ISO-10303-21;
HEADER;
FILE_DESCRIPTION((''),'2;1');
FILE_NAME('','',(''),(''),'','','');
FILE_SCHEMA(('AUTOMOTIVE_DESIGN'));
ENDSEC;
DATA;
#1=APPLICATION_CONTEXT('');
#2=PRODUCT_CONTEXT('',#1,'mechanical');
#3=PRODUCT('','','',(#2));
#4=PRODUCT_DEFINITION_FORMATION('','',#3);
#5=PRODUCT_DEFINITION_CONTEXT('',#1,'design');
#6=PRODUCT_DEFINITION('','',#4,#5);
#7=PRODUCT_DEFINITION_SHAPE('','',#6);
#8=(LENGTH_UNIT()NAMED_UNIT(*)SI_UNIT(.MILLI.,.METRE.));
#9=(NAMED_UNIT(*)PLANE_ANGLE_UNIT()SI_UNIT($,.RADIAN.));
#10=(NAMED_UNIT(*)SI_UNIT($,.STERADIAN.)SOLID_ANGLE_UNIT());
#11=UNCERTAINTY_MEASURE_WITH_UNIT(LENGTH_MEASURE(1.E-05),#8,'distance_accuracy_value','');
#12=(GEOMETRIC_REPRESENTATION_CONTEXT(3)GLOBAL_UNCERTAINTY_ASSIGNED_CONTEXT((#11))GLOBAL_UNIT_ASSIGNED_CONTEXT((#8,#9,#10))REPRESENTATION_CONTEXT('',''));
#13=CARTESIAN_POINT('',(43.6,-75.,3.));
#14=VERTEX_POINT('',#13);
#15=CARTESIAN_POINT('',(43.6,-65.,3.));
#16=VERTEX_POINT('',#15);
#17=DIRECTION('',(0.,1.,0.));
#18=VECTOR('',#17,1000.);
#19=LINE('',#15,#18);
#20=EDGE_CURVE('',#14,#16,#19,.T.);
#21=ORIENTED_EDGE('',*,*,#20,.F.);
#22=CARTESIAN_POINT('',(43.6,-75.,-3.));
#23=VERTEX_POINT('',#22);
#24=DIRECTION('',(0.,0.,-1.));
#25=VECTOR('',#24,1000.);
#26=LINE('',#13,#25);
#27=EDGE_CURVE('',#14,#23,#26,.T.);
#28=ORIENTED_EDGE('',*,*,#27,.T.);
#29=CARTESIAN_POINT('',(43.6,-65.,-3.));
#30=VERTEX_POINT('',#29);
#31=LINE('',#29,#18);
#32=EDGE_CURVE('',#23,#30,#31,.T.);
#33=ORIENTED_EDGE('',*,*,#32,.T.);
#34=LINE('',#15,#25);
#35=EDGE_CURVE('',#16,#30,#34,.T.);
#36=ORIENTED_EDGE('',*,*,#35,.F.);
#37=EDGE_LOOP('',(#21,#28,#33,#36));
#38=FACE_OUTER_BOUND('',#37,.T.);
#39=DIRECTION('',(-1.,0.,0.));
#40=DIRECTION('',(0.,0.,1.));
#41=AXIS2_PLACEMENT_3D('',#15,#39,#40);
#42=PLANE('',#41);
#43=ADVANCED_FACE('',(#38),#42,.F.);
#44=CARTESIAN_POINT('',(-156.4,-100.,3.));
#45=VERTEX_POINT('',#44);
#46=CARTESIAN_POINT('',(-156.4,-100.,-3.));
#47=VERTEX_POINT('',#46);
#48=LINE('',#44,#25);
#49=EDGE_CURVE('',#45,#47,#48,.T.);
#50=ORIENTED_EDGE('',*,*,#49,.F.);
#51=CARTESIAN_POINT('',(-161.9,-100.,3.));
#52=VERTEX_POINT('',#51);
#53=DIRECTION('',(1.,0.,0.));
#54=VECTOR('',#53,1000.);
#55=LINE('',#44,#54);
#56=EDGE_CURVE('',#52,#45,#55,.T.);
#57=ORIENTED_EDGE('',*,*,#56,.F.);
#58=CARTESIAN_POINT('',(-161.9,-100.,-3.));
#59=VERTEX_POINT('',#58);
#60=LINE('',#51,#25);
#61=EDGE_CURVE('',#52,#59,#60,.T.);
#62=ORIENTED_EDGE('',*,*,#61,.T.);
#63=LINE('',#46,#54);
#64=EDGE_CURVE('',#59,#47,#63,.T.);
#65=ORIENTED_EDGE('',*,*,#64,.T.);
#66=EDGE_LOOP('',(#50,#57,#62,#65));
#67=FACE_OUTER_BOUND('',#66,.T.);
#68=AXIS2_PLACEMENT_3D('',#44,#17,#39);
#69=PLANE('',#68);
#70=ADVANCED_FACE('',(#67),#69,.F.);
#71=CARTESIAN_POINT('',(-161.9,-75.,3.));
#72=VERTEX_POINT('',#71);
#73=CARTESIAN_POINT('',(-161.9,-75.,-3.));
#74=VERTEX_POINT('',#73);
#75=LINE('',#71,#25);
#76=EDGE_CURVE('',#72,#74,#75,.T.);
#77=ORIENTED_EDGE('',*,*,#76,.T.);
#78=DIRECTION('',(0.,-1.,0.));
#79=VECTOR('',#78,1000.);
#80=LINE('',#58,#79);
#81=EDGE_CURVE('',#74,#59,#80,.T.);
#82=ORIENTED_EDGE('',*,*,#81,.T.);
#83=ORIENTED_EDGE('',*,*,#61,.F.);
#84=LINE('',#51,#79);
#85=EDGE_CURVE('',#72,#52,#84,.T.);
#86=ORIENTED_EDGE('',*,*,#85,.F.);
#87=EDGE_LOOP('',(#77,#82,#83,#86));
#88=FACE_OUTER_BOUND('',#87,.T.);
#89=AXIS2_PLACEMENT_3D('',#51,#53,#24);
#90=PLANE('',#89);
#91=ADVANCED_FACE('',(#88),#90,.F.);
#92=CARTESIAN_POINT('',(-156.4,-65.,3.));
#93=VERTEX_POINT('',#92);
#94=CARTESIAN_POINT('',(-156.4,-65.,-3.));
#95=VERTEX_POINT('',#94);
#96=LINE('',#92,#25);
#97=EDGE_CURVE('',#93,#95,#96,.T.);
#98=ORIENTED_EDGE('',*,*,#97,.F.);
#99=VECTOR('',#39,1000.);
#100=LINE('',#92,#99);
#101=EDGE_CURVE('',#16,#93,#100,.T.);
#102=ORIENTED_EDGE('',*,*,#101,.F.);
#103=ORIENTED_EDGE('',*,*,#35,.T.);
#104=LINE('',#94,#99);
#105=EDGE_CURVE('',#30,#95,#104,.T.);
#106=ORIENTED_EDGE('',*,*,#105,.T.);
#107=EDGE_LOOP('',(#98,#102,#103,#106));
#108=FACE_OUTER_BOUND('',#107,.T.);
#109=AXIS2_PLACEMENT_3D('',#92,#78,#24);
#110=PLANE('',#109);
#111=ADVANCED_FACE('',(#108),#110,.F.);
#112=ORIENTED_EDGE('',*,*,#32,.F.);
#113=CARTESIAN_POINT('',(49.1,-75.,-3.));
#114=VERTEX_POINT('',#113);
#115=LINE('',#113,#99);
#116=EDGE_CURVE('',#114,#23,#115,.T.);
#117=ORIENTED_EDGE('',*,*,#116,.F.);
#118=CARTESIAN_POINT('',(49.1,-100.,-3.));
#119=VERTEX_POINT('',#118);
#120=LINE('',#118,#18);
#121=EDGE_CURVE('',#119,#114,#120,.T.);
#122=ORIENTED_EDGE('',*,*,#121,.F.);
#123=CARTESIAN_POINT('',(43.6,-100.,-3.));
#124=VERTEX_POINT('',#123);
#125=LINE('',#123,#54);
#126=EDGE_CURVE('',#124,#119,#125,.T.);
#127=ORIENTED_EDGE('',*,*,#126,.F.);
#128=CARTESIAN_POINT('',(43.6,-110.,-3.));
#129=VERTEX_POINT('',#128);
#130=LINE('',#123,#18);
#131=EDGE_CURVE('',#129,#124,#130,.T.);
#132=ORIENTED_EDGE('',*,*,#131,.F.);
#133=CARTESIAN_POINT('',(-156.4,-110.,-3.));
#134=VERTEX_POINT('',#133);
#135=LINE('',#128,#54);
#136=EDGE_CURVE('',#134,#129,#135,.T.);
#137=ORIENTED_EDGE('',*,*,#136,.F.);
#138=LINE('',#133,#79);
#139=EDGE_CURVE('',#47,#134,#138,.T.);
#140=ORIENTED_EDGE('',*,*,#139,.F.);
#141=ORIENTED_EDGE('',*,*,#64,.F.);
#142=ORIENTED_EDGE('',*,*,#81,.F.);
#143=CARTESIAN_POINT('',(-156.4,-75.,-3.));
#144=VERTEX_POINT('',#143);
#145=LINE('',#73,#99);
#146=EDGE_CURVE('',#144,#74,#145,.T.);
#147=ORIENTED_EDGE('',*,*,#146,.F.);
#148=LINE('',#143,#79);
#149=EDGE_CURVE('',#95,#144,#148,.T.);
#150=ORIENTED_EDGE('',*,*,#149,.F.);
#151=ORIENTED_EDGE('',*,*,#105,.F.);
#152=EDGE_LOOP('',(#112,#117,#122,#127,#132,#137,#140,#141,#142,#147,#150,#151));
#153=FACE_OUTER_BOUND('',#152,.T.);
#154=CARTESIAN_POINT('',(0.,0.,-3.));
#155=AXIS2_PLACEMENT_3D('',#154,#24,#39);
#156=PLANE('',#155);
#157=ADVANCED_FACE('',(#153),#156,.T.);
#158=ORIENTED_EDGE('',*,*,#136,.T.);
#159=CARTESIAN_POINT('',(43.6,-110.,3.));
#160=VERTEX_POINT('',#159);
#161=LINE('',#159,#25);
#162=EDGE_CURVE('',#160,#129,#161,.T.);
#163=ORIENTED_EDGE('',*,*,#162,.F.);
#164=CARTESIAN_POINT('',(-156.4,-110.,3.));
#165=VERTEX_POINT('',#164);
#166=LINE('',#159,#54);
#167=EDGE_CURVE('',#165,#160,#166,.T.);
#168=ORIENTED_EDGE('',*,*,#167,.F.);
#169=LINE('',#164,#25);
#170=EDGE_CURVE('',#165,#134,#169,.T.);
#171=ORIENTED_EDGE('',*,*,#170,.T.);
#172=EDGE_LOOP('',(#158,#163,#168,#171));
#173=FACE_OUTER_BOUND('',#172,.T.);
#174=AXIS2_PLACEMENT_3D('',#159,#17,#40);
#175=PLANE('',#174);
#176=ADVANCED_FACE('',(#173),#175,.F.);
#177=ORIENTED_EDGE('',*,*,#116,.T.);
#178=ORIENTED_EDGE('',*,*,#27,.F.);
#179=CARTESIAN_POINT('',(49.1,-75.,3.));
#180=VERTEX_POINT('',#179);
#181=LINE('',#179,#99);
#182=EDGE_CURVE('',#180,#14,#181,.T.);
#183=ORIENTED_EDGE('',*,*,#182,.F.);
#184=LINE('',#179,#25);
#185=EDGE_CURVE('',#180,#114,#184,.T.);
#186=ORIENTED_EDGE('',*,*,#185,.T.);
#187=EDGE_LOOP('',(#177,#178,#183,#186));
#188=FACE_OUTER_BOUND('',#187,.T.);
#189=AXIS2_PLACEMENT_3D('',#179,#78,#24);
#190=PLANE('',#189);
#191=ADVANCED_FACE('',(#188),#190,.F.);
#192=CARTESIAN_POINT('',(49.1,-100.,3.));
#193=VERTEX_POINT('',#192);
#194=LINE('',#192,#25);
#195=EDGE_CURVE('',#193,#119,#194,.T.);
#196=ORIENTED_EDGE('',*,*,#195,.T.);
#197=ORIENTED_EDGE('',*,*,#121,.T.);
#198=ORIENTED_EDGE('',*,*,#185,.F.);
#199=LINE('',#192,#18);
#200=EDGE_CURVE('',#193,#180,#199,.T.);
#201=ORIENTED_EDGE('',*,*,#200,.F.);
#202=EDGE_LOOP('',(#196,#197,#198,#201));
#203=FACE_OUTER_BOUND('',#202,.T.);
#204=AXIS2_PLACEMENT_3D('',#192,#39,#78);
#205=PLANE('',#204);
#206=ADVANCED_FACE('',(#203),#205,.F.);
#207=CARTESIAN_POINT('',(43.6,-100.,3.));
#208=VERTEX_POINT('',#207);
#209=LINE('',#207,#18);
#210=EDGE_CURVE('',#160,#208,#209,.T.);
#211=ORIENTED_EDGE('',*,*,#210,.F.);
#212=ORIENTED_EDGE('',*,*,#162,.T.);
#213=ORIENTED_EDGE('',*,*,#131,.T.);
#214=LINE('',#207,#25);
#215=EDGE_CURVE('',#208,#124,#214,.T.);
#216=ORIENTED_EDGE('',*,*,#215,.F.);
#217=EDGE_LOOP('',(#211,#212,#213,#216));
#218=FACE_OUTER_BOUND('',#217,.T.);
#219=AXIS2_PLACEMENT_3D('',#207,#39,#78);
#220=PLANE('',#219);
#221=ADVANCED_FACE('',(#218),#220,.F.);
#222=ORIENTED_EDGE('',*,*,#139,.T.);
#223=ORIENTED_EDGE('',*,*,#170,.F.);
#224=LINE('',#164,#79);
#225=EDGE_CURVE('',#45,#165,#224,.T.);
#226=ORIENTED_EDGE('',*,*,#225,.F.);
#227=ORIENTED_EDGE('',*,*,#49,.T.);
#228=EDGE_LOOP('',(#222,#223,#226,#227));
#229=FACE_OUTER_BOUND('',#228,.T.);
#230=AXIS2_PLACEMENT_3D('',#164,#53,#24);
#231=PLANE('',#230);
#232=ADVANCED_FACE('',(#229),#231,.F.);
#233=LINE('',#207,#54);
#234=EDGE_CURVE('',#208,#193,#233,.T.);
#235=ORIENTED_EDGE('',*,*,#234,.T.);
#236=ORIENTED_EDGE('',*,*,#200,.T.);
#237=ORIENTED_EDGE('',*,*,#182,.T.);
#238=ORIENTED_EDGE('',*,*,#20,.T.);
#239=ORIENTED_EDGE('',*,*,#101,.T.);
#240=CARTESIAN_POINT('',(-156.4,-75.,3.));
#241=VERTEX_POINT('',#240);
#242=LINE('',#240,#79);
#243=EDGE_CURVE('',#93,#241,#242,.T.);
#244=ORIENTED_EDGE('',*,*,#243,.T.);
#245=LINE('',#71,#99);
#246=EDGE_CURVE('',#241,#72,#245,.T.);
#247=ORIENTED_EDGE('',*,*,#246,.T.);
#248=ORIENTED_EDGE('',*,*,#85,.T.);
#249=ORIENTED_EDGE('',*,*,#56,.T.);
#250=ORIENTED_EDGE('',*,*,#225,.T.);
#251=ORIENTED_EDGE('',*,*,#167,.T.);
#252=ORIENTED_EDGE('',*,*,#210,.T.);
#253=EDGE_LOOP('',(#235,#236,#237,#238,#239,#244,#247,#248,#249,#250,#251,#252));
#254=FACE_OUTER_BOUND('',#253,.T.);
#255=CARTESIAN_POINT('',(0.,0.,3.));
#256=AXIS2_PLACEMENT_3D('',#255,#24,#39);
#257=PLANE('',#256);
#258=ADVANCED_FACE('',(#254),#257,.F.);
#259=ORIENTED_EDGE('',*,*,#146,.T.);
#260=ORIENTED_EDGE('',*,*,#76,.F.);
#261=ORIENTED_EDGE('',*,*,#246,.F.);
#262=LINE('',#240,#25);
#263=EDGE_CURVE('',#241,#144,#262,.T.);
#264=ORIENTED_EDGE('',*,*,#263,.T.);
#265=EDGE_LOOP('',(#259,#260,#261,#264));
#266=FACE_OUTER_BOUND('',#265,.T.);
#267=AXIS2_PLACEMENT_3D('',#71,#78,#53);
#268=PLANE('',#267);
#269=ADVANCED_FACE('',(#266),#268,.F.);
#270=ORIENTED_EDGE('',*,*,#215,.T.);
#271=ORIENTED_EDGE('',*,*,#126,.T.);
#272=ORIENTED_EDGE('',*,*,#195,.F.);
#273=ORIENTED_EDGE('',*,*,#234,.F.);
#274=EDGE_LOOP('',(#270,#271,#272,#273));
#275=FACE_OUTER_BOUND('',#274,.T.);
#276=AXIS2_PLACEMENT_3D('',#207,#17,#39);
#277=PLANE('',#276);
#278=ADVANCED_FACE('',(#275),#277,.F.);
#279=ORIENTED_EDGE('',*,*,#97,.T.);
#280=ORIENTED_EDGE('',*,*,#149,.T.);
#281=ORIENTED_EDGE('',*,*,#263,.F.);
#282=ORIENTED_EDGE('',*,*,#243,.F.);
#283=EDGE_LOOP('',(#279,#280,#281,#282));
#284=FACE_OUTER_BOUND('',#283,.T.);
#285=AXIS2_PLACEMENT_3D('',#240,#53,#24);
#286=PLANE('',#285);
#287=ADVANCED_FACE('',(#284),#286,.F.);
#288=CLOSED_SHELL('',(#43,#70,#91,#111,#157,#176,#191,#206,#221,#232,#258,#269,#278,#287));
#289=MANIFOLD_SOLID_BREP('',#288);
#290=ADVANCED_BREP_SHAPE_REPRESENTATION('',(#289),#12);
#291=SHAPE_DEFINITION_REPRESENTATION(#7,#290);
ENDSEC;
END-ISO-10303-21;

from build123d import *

# Parameters (mm, degrees)
BOSS_EXTRUDE1_DEPTH = 3


with BuildPart() as part:
    # Sketch1 → Boss-Extrude1 (new, symmetric)
    with BuildSketch(Plane.XY):
        Polygon((43.6, -110), (-156.4, -110), (-156.4, -100), (-161.9, -100), (-161.9, -75), (-156.4, -75), (-156.4, -65), (43.6, -65), (43.6, -75), (49.1, -75), (49.1, -100), (43.6, -100), align=None)
    extrude(amount=BOSS_EXTRUDE1_DEPTH, both=True)


solid = part.part
